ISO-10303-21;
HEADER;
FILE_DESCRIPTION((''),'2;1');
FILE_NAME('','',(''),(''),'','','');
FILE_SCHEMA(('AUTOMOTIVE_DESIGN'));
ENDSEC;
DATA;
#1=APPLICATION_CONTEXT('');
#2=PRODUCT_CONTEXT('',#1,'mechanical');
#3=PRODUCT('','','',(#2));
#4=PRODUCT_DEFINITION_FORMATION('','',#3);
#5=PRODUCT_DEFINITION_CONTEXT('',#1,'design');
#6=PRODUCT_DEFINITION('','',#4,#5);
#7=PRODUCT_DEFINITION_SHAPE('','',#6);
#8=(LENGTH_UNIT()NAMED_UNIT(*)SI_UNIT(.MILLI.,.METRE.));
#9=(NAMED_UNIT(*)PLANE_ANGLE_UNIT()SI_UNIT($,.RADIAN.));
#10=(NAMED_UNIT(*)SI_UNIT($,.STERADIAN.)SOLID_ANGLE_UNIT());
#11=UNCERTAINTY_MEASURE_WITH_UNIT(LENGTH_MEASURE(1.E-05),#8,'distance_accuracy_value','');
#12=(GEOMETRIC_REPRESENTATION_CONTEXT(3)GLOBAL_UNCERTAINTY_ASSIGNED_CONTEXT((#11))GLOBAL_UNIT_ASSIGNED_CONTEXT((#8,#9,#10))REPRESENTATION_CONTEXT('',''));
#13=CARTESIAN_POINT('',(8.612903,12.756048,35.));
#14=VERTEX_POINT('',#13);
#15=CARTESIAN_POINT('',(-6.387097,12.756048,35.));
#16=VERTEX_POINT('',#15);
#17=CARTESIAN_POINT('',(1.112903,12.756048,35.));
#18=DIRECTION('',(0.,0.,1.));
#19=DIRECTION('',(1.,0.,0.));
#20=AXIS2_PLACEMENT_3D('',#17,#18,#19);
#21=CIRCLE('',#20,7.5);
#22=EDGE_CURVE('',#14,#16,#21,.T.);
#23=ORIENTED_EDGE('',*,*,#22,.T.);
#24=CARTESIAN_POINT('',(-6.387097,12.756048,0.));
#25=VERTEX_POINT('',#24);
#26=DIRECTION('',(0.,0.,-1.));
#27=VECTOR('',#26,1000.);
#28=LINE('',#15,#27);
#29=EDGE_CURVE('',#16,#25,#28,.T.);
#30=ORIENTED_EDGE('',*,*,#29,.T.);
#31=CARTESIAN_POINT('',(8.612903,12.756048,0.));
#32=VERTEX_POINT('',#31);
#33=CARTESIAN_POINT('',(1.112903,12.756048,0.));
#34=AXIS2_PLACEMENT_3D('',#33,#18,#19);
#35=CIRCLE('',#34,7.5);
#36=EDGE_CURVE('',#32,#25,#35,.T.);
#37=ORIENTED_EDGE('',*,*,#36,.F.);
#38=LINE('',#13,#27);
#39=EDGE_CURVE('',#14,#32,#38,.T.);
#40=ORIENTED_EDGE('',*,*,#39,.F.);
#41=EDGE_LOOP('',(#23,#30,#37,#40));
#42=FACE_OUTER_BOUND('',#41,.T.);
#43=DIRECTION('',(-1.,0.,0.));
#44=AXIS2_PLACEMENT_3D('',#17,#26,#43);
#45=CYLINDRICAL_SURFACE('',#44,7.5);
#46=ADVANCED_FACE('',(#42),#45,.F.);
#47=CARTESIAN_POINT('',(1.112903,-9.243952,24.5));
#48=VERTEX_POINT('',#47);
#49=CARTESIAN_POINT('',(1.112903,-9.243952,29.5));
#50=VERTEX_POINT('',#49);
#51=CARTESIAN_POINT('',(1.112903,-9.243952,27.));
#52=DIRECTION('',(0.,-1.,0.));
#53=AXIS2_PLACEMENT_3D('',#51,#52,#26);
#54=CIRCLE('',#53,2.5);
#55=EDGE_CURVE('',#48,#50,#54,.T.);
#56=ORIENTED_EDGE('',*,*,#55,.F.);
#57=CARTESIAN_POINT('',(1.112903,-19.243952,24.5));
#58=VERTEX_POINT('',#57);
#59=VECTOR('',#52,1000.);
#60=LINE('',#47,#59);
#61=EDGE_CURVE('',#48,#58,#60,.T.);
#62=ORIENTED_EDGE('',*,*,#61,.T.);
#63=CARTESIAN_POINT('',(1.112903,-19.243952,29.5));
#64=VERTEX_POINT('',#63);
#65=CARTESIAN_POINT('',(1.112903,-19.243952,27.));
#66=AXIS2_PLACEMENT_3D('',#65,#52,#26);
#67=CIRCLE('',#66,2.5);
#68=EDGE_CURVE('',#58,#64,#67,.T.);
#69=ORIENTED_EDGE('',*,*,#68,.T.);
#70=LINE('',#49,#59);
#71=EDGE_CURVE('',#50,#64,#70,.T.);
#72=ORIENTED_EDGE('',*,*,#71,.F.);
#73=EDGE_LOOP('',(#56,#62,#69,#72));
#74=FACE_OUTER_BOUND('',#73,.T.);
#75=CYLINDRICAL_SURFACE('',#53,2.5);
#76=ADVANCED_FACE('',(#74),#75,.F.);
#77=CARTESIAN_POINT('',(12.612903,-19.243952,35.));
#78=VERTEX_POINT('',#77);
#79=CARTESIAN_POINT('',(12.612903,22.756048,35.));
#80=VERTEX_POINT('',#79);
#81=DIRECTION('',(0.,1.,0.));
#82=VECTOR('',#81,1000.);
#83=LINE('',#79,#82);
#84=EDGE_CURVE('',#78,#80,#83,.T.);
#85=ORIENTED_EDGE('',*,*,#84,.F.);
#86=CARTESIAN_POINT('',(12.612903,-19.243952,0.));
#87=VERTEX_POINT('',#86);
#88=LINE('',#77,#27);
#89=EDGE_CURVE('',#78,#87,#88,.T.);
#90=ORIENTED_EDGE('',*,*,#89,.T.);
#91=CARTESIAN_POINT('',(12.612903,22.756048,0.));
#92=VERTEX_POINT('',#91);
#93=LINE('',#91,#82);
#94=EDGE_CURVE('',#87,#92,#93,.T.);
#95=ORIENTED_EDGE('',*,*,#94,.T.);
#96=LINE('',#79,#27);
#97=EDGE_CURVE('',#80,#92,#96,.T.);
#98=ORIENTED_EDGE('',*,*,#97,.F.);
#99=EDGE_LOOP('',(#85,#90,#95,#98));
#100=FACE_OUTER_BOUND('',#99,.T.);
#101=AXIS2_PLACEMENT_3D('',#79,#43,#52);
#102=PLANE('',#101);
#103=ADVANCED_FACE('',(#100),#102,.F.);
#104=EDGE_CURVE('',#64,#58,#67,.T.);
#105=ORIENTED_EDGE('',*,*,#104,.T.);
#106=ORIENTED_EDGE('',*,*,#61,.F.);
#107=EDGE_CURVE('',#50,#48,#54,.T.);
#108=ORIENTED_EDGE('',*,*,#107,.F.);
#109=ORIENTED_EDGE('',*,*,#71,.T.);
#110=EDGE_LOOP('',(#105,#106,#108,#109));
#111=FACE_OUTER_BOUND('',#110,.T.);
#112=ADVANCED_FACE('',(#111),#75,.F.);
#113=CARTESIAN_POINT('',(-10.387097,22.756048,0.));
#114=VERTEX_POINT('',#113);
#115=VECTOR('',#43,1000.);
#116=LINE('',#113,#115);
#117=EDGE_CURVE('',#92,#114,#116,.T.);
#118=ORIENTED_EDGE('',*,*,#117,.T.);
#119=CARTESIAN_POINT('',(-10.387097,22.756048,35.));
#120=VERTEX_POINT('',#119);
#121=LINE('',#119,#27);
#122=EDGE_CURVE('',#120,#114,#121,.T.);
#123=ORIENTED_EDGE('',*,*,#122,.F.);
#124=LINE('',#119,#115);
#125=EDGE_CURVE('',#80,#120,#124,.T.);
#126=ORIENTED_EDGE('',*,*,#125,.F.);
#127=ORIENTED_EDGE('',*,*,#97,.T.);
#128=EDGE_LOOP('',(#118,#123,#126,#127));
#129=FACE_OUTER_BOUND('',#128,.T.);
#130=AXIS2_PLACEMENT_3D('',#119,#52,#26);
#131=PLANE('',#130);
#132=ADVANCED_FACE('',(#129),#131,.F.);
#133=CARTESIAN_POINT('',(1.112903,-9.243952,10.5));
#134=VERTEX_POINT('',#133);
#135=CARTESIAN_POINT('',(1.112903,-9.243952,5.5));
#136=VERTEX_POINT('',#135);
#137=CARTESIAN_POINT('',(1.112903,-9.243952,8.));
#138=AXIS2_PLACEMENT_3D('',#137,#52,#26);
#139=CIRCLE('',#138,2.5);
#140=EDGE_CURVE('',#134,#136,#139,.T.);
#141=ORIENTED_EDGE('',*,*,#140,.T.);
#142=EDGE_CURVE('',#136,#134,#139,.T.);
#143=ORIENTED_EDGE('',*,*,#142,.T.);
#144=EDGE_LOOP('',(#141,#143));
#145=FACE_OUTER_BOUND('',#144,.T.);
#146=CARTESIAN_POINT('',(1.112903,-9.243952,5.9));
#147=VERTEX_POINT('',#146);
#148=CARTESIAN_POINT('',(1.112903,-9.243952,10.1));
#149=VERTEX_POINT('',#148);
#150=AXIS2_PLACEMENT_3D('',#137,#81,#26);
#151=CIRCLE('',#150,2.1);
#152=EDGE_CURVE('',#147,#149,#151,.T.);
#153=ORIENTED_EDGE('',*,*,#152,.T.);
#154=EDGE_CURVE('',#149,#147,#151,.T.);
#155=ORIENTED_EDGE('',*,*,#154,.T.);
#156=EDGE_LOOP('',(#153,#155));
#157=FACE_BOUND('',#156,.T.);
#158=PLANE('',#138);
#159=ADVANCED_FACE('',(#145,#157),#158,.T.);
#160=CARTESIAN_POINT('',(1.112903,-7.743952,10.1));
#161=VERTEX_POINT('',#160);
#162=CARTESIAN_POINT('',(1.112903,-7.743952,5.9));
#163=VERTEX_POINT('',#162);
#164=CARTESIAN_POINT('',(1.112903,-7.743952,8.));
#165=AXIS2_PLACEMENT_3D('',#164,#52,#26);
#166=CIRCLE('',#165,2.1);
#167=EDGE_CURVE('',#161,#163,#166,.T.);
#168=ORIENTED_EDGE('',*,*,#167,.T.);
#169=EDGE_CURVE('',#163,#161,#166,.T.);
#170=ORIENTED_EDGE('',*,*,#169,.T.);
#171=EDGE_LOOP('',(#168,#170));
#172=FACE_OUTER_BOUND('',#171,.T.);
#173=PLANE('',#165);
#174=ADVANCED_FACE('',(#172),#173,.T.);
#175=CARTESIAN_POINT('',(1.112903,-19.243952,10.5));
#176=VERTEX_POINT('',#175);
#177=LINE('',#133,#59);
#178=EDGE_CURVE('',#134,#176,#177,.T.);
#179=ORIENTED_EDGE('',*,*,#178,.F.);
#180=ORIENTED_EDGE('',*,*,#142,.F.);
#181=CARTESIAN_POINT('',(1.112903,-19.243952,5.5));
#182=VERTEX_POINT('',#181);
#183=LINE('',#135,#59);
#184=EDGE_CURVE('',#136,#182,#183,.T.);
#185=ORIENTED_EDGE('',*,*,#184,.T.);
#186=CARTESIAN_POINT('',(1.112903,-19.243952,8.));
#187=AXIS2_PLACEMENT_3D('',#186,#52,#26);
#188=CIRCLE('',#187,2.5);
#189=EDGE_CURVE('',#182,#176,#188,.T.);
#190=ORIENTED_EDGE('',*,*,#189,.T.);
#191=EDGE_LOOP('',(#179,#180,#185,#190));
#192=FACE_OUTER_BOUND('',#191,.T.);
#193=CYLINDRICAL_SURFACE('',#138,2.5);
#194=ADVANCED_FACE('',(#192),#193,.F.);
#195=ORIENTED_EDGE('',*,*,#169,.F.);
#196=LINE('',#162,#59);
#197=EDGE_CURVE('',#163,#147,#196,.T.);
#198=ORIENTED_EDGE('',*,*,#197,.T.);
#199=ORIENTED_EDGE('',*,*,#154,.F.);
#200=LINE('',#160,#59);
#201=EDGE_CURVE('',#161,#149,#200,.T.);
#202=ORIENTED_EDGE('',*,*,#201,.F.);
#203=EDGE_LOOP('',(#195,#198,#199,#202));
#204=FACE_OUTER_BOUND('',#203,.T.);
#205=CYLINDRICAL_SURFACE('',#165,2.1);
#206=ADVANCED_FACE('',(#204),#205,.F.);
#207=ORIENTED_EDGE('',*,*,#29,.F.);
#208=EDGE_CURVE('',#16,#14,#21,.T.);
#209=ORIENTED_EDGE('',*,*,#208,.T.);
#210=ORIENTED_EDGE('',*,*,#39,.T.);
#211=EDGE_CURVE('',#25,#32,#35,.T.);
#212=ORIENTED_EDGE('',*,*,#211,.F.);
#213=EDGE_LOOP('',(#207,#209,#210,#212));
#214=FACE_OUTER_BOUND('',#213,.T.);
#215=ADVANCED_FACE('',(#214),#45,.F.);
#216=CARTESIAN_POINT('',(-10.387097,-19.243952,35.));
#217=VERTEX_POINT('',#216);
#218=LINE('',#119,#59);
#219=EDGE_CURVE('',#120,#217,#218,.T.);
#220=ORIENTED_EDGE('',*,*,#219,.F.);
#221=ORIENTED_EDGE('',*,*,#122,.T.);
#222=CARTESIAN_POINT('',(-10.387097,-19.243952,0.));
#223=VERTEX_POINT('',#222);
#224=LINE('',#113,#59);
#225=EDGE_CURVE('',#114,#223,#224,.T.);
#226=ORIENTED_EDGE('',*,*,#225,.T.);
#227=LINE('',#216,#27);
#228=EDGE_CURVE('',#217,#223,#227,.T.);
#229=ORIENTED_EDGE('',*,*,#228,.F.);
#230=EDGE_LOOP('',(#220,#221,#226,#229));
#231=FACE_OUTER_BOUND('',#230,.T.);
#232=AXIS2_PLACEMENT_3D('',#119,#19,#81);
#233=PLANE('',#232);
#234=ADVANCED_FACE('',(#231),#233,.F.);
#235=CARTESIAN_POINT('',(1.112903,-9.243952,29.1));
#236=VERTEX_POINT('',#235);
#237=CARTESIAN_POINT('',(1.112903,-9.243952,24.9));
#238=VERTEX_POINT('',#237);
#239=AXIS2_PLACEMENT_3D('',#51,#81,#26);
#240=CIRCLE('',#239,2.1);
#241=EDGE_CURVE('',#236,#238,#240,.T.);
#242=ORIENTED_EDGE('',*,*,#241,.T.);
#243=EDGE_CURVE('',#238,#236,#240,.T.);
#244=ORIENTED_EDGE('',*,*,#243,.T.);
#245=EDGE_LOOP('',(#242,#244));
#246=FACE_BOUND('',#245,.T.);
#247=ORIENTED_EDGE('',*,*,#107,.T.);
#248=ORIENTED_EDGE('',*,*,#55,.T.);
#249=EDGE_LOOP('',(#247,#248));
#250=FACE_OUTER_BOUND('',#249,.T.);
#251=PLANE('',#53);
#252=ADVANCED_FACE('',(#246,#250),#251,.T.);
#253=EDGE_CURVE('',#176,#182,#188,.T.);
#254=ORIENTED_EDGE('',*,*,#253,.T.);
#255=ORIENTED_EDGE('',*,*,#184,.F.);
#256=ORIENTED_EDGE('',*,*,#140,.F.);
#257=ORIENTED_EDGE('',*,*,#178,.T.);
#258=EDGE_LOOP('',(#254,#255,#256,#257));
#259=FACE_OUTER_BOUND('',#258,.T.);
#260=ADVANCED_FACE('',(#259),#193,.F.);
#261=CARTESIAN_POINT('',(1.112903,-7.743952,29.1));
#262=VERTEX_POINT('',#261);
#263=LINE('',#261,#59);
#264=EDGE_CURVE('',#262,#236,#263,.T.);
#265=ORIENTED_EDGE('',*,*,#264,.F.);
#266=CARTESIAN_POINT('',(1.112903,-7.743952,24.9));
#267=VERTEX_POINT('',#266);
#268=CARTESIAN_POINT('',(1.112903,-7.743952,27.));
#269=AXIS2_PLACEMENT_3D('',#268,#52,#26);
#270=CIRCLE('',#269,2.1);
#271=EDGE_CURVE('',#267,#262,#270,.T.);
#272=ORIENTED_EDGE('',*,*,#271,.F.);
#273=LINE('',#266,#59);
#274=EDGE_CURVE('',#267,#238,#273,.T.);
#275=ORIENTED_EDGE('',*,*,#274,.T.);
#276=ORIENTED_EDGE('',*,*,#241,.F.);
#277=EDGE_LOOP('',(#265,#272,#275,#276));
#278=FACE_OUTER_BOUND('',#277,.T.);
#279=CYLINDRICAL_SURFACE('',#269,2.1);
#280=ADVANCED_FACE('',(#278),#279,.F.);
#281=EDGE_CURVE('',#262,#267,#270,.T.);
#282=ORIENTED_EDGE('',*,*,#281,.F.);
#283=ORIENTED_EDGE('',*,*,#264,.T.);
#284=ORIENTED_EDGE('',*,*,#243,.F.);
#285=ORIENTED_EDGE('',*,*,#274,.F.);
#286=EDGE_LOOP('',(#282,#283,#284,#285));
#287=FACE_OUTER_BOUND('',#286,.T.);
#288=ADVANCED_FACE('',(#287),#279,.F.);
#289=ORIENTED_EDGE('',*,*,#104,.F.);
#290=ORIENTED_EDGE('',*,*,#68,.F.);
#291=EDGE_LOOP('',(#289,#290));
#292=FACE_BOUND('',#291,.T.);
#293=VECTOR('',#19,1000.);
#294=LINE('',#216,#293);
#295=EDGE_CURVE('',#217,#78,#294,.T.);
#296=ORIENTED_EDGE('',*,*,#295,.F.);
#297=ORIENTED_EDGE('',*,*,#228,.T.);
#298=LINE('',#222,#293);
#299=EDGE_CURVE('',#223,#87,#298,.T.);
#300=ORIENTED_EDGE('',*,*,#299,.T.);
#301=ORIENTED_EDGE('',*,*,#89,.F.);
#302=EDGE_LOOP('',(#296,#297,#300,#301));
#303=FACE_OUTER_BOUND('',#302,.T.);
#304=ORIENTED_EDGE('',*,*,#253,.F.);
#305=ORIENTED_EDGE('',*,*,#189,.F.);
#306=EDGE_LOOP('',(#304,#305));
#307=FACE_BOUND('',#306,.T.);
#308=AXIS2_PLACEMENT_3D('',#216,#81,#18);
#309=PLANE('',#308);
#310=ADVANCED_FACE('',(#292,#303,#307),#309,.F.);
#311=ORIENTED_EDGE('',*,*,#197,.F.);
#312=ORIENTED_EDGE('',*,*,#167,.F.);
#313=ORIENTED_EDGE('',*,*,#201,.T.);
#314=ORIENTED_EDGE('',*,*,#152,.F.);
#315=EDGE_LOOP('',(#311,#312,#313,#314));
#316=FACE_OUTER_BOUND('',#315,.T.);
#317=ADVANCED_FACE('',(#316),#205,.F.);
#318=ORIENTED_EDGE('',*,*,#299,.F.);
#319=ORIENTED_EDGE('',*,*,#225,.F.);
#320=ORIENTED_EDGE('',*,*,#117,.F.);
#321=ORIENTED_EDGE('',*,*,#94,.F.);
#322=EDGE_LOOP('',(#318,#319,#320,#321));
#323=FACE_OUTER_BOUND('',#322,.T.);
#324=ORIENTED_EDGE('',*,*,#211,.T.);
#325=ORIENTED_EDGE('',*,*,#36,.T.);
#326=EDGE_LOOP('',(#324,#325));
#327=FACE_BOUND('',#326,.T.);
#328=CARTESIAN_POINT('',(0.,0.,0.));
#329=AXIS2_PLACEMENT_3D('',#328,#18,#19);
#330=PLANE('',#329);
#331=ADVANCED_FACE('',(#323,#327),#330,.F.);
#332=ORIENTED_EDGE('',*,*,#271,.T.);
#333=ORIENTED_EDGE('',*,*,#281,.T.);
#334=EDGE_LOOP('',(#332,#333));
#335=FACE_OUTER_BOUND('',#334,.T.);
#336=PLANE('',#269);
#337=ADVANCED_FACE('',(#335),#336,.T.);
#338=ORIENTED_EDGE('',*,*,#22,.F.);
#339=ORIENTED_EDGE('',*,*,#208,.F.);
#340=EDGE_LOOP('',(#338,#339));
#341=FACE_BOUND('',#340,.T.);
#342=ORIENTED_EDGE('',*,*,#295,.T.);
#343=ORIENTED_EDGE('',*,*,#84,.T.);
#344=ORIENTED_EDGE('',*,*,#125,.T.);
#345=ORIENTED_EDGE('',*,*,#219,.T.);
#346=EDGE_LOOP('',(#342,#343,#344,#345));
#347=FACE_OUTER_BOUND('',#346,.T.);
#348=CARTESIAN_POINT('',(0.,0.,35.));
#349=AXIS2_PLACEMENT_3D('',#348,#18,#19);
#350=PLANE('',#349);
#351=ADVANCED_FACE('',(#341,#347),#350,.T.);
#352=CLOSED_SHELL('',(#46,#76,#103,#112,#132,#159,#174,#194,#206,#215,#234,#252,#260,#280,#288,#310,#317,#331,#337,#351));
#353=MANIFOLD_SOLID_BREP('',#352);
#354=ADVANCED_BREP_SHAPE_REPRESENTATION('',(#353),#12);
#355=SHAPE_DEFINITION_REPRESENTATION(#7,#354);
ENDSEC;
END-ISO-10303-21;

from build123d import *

# Parameters (mm, degrees)
SKETCH_1_W          = 23
SKETCH_1_H          = 42
SKETCH_1_R          = 7.5
EXTRUDE_1_DEPTH     = 35
SKETCH_2_R          = 2.1
CUT_EXTRUDE_1_DEPTH = 11.5
SKETCH_3_R          = 2.5
CUT_EXTRUDE_2_DEPTH = 10


with BuildPart() as part:
    # 草图1 → 凸台-拉伸1 (new body)
    with BuildSketch(Plane.XY):
        with Locations((1.112903226, 1.756048387)):
            Rectangle(SKETCH_1_W, SKETCH_1_H)
        with Locations((1.112903226, 12.756048387)):
            Circle(SKETCH_1_R, mode=Mode.SUBTRACT)
    extrude(amount=EXTRUDE_1_DEPTH)

    # 草图2 → 切除-拉伸1 (cut)
    with BuildSketch(Plane.XZ.offset(19.243951613)):
        with Locations(Location((1.112903226, 27, 0), (0, 0, 270))):
            Circle(SKETCH_2_R)
        with Locations(Location((1.112903226, 8, 0), (0, 0, 270))):
            Circle(SKETCH_2_R)
    extrude(amount=-CUT_EXTRUDE_1_DEPTH, mode=Mode.SUBTRACT)

    # 草图3 → 切除-拉伸2 (cut)
    with BuildSketch(Plane.XZ.offset(19.243951613)):
        with Locations(Location((1.112903226, 27, 0), (0, 0, 270))):
            Circle(SKETCH_3_R)
        with Locations(Location((1.112903226, 8, 0), (0, 0, 270))):
            Circle(SKETCH_3_R)
    extrude(amount=-CUT_EXTRUDE_2_DEPTH, mode=Mode.SUBTRACT)


solid = part.part
